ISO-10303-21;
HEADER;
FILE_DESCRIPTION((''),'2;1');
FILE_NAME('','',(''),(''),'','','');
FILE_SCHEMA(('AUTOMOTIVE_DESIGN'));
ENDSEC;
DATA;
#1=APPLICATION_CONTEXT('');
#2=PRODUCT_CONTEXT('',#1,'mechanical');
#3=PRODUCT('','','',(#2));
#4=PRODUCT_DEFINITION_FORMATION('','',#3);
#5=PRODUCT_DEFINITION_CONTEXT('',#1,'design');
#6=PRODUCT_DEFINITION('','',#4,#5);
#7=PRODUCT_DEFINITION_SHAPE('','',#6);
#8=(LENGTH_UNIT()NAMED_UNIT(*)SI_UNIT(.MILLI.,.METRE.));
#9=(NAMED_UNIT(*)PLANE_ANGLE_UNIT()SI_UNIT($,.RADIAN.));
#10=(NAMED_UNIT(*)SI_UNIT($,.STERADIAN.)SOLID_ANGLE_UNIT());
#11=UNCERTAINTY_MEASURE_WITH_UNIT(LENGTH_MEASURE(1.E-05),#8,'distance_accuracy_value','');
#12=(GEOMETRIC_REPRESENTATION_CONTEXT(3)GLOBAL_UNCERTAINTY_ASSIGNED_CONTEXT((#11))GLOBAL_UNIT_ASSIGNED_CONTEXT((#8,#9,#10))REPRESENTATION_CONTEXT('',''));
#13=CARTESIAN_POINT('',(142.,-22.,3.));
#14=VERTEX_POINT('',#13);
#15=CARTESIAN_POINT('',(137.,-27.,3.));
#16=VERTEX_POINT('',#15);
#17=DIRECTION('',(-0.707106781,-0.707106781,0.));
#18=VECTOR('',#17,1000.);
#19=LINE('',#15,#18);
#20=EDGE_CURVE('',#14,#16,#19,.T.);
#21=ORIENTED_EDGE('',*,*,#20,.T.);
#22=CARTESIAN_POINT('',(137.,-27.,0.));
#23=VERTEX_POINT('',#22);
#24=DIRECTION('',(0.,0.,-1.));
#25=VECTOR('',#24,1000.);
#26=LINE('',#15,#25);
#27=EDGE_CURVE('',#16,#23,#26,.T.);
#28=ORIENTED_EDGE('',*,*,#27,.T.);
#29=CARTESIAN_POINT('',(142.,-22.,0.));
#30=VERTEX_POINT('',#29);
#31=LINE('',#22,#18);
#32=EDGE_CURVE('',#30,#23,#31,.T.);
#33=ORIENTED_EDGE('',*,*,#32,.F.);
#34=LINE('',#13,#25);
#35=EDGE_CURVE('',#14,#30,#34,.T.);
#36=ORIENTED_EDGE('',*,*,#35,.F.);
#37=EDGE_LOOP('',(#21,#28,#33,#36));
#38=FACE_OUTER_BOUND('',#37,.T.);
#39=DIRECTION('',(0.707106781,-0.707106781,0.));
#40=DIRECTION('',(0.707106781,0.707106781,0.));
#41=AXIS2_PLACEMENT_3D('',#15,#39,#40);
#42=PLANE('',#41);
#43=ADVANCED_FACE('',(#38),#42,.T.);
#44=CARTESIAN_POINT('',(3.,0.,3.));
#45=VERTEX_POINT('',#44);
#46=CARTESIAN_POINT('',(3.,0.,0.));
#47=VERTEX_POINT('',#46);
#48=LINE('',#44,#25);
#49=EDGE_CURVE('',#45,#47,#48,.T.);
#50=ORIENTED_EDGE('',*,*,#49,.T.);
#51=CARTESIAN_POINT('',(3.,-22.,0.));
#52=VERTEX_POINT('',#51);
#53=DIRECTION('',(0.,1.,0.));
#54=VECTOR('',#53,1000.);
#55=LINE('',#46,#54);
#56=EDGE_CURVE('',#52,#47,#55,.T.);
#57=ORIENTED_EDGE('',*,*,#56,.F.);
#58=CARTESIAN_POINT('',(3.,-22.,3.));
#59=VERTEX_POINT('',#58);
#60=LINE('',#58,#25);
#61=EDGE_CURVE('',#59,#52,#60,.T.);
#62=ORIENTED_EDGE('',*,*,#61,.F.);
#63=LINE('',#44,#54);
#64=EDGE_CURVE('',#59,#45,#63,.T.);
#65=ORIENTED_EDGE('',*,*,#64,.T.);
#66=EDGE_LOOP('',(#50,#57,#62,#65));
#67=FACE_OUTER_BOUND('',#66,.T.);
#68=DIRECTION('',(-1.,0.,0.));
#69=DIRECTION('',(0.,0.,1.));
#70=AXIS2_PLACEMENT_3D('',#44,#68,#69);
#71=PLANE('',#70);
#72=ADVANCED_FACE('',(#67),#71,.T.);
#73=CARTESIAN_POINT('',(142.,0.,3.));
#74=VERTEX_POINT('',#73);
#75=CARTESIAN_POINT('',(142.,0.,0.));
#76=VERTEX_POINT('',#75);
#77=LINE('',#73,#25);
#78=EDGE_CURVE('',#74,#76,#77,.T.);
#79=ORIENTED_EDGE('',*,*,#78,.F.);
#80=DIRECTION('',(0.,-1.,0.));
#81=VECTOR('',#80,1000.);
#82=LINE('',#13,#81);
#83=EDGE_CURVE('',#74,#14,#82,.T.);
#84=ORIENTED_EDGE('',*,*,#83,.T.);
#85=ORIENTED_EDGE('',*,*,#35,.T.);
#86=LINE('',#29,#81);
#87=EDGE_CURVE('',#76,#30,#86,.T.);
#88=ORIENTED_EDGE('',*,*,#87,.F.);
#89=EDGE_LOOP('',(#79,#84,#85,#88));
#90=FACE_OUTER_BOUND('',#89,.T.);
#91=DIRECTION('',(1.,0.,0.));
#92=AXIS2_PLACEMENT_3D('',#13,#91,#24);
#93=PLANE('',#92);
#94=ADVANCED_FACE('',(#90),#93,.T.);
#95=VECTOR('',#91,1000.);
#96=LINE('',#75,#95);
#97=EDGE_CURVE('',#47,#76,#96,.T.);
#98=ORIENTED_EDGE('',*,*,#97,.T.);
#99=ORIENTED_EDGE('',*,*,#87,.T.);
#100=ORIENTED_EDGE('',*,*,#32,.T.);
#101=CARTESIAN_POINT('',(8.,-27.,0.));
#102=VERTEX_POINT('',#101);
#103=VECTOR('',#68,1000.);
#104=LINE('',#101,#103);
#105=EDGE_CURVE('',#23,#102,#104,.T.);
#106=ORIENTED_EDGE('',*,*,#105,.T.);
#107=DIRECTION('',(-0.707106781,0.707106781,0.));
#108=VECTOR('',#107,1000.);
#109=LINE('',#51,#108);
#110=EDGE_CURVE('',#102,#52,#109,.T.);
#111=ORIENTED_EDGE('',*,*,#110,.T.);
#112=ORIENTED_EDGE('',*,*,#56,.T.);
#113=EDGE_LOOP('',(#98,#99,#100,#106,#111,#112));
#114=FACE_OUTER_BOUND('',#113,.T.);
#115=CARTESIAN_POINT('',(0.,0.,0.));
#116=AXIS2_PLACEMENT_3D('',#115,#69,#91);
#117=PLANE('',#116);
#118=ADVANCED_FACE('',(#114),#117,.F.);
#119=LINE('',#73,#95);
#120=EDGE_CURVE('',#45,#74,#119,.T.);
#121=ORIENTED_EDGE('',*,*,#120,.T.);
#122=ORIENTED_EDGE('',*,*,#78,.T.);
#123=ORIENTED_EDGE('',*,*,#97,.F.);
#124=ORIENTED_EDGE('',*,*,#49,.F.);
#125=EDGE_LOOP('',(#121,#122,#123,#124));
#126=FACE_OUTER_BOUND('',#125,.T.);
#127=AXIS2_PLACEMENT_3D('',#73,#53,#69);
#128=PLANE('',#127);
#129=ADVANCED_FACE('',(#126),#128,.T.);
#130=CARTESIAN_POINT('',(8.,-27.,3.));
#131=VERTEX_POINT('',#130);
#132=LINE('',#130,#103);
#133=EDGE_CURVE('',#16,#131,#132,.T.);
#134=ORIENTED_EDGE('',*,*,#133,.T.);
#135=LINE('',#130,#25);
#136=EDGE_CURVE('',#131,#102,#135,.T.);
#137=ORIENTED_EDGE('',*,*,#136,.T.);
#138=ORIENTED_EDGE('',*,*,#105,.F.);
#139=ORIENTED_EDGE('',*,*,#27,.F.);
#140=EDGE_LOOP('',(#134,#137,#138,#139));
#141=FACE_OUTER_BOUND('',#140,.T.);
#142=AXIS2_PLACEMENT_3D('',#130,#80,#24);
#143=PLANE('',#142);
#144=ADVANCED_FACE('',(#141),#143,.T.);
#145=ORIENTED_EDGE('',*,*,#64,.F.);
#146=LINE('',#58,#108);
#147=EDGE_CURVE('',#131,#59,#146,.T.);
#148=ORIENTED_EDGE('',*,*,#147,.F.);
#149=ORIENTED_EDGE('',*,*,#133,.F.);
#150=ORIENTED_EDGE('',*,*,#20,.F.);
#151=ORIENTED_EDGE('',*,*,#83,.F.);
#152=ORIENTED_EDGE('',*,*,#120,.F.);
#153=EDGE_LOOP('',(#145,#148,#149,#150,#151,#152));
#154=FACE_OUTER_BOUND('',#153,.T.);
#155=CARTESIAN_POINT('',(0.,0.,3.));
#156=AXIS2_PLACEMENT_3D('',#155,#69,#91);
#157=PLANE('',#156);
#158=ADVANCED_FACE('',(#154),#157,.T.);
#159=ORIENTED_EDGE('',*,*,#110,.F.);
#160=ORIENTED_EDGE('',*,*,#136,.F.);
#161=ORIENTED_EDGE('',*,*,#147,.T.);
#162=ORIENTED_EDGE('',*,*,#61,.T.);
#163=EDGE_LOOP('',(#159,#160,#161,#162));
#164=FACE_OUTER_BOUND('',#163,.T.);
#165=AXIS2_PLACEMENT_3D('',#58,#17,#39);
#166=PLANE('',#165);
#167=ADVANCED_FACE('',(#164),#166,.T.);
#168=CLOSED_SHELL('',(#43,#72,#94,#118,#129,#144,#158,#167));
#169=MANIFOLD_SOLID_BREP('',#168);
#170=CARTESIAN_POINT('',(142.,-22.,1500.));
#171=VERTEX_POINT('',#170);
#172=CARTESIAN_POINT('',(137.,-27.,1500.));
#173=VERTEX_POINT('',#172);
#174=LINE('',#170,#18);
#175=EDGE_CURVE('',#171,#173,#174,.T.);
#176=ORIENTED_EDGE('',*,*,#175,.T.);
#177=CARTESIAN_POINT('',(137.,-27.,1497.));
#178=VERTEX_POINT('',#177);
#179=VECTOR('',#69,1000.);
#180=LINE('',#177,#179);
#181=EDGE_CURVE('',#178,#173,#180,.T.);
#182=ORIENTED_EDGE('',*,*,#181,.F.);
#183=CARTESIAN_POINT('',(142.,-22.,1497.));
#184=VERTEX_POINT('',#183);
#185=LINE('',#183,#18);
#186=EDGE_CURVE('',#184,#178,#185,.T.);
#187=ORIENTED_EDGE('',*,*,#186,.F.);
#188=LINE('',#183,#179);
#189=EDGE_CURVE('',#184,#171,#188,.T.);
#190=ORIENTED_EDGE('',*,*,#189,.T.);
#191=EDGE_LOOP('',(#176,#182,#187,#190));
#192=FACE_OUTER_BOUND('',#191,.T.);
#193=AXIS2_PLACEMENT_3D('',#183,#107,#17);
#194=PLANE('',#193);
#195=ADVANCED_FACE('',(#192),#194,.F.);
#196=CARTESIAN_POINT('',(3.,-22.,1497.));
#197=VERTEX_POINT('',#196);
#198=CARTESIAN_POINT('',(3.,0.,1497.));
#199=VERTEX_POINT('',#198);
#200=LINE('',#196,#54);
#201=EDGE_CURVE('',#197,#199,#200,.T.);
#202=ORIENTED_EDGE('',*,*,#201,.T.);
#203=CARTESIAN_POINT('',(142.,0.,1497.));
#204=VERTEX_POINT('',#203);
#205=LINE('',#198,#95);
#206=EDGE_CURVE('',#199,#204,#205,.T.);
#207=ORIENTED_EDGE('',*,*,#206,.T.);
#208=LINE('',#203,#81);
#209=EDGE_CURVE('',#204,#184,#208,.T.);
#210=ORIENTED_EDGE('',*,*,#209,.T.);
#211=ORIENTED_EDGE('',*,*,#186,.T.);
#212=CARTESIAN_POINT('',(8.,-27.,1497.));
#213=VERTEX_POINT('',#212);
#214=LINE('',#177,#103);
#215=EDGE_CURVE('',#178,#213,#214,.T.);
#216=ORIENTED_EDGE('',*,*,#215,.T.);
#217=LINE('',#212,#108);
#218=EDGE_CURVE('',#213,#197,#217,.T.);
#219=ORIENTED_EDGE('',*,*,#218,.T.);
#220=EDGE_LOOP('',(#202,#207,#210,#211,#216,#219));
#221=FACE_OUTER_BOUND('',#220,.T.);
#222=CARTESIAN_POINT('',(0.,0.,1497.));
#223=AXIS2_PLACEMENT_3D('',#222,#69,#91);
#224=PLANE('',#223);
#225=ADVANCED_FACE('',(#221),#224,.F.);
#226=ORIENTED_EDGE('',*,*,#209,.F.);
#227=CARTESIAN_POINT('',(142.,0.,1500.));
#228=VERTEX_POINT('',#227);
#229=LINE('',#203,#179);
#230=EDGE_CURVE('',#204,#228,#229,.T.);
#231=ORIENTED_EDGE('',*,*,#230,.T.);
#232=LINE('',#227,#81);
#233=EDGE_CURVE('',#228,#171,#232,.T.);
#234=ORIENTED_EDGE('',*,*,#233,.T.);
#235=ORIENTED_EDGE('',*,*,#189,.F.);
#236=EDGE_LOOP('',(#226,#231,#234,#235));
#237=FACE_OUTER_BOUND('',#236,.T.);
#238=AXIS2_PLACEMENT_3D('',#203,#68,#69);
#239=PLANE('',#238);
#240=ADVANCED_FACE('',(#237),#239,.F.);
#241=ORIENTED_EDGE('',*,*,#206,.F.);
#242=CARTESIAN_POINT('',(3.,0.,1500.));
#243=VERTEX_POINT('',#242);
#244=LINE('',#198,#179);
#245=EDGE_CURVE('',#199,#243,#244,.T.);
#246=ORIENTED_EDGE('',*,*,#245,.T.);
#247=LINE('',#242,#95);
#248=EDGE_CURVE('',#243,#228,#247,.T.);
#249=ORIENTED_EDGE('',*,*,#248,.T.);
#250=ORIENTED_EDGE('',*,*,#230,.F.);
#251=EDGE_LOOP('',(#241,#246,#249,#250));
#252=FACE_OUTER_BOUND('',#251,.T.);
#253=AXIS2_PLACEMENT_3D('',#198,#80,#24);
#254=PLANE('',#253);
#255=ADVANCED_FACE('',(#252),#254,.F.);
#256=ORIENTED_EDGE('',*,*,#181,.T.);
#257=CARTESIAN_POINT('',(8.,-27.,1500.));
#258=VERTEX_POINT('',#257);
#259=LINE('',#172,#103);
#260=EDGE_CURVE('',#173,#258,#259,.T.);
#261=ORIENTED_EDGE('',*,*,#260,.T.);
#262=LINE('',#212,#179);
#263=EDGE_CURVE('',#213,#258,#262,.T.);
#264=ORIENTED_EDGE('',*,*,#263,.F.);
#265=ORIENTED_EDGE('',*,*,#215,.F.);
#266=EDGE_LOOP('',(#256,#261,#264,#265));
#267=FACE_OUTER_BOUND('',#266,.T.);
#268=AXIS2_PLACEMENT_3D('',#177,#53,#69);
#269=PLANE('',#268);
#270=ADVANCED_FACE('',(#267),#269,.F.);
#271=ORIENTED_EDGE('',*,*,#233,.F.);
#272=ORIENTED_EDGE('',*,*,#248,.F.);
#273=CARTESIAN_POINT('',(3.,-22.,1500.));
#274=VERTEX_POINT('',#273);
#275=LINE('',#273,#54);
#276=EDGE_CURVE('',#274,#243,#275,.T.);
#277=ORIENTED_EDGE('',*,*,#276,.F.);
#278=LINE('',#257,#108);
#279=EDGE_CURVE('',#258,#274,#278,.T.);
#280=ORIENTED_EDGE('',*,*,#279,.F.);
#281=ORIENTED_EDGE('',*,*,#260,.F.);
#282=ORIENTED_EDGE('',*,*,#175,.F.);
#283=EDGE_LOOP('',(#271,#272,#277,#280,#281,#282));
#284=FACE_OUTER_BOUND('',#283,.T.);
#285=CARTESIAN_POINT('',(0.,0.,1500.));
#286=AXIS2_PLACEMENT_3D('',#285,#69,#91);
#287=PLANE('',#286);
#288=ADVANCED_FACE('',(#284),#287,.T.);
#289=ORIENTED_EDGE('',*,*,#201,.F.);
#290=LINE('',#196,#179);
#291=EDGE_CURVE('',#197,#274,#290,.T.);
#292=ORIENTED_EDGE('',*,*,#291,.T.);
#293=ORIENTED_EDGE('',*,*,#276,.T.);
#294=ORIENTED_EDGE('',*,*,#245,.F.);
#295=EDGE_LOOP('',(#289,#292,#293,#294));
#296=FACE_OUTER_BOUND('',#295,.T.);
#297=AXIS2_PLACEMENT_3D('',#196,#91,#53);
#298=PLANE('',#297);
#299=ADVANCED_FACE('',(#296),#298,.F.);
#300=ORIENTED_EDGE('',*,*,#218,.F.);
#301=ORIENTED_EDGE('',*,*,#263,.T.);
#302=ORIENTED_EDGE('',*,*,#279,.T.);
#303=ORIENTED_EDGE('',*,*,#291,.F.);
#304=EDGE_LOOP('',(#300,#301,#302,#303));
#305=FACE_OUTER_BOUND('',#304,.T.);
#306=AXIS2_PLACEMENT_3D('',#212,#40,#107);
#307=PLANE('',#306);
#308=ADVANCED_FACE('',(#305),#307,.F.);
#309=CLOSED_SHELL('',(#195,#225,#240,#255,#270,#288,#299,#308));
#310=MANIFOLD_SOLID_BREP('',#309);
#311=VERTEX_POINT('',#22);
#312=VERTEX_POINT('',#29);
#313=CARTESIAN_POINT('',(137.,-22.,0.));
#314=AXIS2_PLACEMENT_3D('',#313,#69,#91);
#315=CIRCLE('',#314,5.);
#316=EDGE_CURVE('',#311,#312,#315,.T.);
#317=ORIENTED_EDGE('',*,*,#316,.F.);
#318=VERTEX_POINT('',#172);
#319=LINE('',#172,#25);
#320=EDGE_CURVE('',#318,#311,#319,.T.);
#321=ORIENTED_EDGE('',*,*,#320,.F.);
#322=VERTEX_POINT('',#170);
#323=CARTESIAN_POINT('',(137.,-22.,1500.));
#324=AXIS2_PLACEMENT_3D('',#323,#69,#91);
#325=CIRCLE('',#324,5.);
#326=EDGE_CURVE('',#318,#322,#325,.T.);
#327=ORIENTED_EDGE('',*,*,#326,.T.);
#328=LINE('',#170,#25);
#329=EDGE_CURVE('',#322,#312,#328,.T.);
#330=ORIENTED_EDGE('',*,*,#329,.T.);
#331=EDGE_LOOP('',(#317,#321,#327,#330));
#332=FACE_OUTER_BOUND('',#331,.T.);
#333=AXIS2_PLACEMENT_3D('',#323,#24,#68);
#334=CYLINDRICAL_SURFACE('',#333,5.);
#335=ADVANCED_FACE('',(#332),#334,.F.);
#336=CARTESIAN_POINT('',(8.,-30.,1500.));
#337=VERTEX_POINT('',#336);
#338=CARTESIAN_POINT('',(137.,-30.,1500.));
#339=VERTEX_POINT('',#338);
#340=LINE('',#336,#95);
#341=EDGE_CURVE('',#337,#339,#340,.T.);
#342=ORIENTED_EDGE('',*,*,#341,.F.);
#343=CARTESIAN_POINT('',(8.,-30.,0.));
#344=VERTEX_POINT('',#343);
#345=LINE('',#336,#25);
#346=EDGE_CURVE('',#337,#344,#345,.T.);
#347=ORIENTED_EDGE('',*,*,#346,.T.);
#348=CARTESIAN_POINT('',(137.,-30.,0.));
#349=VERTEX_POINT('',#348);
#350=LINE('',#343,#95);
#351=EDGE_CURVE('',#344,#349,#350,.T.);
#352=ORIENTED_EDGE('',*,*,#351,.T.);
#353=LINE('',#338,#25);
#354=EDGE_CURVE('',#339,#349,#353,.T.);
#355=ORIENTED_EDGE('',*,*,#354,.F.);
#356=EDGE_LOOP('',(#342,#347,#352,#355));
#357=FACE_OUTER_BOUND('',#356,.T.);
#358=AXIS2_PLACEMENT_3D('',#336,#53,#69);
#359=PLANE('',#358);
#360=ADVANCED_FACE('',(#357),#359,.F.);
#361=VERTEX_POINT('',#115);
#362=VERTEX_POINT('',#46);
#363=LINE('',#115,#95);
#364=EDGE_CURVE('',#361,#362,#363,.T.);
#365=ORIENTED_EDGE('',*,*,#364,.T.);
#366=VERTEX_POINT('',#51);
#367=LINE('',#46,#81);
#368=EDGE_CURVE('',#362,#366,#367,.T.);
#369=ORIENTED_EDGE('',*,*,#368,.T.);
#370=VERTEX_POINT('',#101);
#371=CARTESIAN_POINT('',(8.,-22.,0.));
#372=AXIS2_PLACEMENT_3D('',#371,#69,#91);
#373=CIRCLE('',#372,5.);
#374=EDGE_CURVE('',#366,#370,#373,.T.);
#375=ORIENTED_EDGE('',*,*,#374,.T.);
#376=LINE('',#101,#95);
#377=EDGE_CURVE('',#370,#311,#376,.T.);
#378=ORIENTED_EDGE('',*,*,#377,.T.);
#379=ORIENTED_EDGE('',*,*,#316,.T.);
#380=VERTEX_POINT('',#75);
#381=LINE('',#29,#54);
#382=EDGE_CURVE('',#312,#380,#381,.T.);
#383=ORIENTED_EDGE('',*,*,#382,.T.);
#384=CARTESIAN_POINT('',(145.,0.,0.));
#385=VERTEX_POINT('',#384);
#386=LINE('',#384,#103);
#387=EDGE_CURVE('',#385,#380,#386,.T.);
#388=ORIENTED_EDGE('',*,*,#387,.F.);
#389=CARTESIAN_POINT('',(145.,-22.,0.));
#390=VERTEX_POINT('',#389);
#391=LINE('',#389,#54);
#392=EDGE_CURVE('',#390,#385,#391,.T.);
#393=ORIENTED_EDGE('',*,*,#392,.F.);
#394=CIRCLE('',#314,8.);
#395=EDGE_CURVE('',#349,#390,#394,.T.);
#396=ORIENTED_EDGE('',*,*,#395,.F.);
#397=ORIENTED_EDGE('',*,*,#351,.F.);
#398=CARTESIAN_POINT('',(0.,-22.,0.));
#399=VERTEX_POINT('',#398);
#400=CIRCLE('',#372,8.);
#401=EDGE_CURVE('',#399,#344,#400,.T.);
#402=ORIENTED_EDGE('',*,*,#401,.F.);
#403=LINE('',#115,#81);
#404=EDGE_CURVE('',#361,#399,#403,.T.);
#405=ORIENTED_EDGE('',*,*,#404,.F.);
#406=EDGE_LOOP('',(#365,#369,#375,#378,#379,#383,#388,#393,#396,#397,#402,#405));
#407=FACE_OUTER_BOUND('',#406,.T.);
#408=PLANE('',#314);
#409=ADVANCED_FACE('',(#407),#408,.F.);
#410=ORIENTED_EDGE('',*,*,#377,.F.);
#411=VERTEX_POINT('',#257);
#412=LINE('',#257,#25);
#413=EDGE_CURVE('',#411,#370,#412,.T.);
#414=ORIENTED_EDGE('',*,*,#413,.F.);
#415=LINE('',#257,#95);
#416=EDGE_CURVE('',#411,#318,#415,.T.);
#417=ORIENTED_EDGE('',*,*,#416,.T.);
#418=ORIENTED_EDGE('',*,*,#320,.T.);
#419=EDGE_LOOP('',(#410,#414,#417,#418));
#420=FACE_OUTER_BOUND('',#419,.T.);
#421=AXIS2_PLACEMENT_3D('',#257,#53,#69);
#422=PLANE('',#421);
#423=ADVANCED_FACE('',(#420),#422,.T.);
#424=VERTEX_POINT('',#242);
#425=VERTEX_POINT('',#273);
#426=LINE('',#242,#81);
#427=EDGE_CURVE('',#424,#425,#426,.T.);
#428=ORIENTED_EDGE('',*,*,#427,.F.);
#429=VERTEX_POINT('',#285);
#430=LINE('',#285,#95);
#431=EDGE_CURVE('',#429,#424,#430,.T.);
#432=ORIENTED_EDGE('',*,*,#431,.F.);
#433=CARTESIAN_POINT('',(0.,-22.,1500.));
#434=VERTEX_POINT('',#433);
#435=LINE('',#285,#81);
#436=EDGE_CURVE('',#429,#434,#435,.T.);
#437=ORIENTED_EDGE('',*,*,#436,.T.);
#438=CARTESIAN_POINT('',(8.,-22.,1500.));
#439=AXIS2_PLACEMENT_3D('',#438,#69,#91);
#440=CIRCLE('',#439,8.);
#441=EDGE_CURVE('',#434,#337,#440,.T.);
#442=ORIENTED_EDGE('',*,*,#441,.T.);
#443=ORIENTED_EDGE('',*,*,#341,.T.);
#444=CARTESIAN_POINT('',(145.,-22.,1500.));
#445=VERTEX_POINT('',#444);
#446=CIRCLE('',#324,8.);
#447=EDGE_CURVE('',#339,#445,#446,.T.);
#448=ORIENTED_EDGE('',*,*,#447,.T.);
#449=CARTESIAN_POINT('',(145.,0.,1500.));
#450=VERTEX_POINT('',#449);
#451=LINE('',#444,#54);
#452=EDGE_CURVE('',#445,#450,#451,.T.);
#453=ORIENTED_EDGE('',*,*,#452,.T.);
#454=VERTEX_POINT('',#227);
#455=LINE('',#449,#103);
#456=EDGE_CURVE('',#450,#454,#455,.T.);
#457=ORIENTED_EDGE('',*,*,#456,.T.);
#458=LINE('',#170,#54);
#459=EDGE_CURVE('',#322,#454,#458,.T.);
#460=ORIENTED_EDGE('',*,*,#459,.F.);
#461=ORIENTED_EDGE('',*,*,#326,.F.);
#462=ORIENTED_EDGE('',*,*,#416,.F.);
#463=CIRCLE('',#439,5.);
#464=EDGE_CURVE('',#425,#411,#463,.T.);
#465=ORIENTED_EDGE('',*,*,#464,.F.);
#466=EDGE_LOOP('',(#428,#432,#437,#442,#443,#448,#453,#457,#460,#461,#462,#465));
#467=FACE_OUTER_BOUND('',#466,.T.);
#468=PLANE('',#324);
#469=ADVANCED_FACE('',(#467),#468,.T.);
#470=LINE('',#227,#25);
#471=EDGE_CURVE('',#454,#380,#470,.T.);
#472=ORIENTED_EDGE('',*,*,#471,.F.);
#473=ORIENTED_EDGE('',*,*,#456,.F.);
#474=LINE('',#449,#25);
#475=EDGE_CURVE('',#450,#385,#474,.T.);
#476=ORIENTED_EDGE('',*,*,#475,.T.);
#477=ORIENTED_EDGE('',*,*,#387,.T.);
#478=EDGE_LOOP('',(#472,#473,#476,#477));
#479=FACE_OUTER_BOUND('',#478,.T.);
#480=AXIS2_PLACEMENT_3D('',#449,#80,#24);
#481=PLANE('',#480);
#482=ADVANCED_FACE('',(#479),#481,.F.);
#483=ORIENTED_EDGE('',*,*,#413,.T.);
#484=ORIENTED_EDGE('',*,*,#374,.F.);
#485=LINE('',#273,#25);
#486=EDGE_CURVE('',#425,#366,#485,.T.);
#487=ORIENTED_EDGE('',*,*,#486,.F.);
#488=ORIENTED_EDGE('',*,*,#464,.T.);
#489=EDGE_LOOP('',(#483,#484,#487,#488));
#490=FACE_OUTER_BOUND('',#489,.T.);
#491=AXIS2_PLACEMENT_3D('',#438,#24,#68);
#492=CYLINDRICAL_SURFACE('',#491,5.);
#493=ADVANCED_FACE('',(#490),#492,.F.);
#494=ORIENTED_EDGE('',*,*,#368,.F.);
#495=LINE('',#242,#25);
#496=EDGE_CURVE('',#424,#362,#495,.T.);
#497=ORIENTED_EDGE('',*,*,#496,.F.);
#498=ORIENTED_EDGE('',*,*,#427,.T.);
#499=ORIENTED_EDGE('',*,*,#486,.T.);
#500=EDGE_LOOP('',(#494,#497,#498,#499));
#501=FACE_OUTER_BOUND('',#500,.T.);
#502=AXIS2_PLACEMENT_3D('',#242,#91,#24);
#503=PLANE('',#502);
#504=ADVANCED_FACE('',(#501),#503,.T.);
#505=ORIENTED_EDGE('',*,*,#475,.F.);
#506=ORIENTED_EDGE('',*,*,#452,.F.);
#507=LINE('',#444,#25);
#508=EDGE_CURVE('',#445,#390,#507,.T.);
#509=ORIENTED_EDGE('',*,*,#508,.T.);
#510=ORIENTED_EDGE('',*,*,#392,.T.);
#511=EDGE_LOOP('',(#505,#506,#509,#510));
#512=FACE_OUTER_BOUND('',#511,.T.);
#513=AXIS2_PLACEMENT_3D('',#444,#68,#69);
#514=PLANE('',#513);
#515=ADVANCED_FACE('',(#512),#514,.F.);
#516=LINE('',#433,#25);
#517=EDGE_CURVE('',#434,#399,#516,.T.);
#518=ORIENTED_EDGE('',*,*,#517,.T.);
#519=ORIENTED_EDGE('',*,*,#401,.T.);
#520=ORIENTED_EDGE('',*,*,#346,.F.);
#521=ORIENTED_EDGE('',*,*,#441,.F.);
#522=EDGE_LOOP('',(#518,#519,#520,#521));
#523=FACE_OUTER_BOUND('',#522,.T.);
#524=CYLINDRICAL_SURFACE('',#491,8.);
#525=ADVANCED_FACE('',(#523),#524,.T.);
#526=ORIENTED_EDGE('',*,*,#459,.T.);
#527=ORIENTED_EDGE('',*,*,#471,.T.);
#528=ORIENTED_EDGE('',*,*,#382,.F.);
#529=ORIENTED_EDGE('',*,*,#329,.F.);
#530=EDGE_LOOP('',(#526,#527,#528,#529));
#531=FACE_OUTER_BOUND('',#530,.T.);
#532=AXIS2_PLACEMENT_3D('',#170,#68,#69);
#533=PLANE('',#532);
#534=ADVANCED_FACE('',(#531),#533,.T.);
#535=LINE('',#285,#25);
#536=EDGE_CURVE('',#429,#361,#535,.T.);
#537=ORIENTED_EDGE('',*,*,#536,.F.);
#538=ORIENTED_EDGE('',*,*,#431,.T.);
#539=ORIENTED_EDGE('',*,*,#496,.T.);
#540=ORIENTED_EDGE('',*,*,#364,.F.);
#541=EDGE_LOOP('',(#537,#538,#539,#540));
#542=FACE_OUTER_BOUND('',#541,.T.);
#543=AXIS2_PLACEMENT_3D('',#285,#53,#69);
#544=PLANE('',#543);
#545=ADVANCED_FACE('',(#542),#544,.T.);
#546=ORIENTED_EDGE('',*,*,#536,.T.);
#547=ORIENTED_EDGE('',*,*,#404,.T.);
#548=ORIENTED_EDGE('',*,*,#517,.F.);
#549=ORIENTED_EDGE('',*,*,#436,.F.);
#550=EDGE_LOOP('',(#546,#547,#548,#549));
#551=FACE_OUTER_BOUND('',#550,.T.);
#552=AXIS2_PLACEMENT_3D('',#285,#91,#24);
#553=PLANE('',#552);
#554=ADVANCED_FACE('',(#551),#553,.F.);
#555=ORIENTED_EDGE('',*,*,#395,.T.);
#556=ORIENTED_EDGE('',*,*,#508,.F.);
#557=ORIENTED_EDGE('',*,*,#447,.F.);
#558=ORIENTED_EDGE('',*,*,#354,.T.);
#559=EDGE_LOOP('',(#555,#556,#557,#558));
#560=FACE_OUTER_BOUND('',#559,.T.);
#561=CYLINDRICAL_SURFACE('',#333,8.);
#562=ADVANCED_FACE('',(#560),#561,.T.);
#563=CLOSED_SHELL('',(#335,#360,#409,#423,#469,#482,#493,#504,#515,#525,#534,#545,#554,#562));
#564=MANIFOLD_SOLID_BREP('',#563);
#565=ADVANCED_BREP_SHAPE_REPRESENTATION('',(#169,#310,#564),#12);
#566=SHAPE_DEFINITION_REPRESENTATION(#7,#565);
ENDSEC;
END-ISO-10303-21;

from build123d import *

# Parameters (mm, degrees)
BOSS_EXTRUDE1_DEPTH = 1500
BOSS_EXTRUDE2_DEPTH = 3
BOSS_EXTRUDE3_DEPTH = 3


with BuildPart() as part:
    # Sketch1 → Boss-Extrude1 (new body)
    with BuildSketch(Plane.XY):
        with BuildLine():
            Line((0, 0), (0, -22))
            ThreePointArc((0, -22), (2.343145751, -27.656854249), (8, -30))
            Line((8, -30), (137, -30))
            ThreePointArc((137, -30), (142.656854249, -27.656854249), (145, -22))
            Line((145, -22), (145, 0))
            Line((145, 0), (142, 0))
            Line((142, 0), (142, -22))
            ThreePointArc((142, -22), (140.535533906, -25.535533906), (137, -27))
            Line((137, -27), (8, -27))
            ThreePointArc((8, -27), (4.464466094, -25.535533906), (3, -22))
            Line((3, -22), (3, 0))
            Line((3, 0), (0, 0))
        make_face()
    extrude(amount=BOSS_EXTRUDE1_DEPTH)


with BuildPart() as body_2:
    # Sketch3 → Boss-Extrude2 (new body)
    with BuildSketch(Plane.XY.offset(1500)):
        Polygon((3, 0), (142, 0), (142, -22), (137, -27), (8, -27), (3, -22), align=None)
    extrude(amount=-BOSS_EXTRUDE2_DEPTH)


with BuildPart() as body_3:
    # Sketch4 → Boss-Extrude3 (new body)
    with BuildSketch(Plane(origin=(0, 0, 0), x_dir=(-1, 0, 0), z_dir=(0, 0, -1))):
        Polygon((-142, 0), (-3, 0), (-3, -22), (-8, -27), (-137, -27), (-142, -22), align=None)
    extrude(amount=-BOSS_EXTRUDE3_DEPTH)


solid = Compound([part.part, body_2.part, body_3.part])
